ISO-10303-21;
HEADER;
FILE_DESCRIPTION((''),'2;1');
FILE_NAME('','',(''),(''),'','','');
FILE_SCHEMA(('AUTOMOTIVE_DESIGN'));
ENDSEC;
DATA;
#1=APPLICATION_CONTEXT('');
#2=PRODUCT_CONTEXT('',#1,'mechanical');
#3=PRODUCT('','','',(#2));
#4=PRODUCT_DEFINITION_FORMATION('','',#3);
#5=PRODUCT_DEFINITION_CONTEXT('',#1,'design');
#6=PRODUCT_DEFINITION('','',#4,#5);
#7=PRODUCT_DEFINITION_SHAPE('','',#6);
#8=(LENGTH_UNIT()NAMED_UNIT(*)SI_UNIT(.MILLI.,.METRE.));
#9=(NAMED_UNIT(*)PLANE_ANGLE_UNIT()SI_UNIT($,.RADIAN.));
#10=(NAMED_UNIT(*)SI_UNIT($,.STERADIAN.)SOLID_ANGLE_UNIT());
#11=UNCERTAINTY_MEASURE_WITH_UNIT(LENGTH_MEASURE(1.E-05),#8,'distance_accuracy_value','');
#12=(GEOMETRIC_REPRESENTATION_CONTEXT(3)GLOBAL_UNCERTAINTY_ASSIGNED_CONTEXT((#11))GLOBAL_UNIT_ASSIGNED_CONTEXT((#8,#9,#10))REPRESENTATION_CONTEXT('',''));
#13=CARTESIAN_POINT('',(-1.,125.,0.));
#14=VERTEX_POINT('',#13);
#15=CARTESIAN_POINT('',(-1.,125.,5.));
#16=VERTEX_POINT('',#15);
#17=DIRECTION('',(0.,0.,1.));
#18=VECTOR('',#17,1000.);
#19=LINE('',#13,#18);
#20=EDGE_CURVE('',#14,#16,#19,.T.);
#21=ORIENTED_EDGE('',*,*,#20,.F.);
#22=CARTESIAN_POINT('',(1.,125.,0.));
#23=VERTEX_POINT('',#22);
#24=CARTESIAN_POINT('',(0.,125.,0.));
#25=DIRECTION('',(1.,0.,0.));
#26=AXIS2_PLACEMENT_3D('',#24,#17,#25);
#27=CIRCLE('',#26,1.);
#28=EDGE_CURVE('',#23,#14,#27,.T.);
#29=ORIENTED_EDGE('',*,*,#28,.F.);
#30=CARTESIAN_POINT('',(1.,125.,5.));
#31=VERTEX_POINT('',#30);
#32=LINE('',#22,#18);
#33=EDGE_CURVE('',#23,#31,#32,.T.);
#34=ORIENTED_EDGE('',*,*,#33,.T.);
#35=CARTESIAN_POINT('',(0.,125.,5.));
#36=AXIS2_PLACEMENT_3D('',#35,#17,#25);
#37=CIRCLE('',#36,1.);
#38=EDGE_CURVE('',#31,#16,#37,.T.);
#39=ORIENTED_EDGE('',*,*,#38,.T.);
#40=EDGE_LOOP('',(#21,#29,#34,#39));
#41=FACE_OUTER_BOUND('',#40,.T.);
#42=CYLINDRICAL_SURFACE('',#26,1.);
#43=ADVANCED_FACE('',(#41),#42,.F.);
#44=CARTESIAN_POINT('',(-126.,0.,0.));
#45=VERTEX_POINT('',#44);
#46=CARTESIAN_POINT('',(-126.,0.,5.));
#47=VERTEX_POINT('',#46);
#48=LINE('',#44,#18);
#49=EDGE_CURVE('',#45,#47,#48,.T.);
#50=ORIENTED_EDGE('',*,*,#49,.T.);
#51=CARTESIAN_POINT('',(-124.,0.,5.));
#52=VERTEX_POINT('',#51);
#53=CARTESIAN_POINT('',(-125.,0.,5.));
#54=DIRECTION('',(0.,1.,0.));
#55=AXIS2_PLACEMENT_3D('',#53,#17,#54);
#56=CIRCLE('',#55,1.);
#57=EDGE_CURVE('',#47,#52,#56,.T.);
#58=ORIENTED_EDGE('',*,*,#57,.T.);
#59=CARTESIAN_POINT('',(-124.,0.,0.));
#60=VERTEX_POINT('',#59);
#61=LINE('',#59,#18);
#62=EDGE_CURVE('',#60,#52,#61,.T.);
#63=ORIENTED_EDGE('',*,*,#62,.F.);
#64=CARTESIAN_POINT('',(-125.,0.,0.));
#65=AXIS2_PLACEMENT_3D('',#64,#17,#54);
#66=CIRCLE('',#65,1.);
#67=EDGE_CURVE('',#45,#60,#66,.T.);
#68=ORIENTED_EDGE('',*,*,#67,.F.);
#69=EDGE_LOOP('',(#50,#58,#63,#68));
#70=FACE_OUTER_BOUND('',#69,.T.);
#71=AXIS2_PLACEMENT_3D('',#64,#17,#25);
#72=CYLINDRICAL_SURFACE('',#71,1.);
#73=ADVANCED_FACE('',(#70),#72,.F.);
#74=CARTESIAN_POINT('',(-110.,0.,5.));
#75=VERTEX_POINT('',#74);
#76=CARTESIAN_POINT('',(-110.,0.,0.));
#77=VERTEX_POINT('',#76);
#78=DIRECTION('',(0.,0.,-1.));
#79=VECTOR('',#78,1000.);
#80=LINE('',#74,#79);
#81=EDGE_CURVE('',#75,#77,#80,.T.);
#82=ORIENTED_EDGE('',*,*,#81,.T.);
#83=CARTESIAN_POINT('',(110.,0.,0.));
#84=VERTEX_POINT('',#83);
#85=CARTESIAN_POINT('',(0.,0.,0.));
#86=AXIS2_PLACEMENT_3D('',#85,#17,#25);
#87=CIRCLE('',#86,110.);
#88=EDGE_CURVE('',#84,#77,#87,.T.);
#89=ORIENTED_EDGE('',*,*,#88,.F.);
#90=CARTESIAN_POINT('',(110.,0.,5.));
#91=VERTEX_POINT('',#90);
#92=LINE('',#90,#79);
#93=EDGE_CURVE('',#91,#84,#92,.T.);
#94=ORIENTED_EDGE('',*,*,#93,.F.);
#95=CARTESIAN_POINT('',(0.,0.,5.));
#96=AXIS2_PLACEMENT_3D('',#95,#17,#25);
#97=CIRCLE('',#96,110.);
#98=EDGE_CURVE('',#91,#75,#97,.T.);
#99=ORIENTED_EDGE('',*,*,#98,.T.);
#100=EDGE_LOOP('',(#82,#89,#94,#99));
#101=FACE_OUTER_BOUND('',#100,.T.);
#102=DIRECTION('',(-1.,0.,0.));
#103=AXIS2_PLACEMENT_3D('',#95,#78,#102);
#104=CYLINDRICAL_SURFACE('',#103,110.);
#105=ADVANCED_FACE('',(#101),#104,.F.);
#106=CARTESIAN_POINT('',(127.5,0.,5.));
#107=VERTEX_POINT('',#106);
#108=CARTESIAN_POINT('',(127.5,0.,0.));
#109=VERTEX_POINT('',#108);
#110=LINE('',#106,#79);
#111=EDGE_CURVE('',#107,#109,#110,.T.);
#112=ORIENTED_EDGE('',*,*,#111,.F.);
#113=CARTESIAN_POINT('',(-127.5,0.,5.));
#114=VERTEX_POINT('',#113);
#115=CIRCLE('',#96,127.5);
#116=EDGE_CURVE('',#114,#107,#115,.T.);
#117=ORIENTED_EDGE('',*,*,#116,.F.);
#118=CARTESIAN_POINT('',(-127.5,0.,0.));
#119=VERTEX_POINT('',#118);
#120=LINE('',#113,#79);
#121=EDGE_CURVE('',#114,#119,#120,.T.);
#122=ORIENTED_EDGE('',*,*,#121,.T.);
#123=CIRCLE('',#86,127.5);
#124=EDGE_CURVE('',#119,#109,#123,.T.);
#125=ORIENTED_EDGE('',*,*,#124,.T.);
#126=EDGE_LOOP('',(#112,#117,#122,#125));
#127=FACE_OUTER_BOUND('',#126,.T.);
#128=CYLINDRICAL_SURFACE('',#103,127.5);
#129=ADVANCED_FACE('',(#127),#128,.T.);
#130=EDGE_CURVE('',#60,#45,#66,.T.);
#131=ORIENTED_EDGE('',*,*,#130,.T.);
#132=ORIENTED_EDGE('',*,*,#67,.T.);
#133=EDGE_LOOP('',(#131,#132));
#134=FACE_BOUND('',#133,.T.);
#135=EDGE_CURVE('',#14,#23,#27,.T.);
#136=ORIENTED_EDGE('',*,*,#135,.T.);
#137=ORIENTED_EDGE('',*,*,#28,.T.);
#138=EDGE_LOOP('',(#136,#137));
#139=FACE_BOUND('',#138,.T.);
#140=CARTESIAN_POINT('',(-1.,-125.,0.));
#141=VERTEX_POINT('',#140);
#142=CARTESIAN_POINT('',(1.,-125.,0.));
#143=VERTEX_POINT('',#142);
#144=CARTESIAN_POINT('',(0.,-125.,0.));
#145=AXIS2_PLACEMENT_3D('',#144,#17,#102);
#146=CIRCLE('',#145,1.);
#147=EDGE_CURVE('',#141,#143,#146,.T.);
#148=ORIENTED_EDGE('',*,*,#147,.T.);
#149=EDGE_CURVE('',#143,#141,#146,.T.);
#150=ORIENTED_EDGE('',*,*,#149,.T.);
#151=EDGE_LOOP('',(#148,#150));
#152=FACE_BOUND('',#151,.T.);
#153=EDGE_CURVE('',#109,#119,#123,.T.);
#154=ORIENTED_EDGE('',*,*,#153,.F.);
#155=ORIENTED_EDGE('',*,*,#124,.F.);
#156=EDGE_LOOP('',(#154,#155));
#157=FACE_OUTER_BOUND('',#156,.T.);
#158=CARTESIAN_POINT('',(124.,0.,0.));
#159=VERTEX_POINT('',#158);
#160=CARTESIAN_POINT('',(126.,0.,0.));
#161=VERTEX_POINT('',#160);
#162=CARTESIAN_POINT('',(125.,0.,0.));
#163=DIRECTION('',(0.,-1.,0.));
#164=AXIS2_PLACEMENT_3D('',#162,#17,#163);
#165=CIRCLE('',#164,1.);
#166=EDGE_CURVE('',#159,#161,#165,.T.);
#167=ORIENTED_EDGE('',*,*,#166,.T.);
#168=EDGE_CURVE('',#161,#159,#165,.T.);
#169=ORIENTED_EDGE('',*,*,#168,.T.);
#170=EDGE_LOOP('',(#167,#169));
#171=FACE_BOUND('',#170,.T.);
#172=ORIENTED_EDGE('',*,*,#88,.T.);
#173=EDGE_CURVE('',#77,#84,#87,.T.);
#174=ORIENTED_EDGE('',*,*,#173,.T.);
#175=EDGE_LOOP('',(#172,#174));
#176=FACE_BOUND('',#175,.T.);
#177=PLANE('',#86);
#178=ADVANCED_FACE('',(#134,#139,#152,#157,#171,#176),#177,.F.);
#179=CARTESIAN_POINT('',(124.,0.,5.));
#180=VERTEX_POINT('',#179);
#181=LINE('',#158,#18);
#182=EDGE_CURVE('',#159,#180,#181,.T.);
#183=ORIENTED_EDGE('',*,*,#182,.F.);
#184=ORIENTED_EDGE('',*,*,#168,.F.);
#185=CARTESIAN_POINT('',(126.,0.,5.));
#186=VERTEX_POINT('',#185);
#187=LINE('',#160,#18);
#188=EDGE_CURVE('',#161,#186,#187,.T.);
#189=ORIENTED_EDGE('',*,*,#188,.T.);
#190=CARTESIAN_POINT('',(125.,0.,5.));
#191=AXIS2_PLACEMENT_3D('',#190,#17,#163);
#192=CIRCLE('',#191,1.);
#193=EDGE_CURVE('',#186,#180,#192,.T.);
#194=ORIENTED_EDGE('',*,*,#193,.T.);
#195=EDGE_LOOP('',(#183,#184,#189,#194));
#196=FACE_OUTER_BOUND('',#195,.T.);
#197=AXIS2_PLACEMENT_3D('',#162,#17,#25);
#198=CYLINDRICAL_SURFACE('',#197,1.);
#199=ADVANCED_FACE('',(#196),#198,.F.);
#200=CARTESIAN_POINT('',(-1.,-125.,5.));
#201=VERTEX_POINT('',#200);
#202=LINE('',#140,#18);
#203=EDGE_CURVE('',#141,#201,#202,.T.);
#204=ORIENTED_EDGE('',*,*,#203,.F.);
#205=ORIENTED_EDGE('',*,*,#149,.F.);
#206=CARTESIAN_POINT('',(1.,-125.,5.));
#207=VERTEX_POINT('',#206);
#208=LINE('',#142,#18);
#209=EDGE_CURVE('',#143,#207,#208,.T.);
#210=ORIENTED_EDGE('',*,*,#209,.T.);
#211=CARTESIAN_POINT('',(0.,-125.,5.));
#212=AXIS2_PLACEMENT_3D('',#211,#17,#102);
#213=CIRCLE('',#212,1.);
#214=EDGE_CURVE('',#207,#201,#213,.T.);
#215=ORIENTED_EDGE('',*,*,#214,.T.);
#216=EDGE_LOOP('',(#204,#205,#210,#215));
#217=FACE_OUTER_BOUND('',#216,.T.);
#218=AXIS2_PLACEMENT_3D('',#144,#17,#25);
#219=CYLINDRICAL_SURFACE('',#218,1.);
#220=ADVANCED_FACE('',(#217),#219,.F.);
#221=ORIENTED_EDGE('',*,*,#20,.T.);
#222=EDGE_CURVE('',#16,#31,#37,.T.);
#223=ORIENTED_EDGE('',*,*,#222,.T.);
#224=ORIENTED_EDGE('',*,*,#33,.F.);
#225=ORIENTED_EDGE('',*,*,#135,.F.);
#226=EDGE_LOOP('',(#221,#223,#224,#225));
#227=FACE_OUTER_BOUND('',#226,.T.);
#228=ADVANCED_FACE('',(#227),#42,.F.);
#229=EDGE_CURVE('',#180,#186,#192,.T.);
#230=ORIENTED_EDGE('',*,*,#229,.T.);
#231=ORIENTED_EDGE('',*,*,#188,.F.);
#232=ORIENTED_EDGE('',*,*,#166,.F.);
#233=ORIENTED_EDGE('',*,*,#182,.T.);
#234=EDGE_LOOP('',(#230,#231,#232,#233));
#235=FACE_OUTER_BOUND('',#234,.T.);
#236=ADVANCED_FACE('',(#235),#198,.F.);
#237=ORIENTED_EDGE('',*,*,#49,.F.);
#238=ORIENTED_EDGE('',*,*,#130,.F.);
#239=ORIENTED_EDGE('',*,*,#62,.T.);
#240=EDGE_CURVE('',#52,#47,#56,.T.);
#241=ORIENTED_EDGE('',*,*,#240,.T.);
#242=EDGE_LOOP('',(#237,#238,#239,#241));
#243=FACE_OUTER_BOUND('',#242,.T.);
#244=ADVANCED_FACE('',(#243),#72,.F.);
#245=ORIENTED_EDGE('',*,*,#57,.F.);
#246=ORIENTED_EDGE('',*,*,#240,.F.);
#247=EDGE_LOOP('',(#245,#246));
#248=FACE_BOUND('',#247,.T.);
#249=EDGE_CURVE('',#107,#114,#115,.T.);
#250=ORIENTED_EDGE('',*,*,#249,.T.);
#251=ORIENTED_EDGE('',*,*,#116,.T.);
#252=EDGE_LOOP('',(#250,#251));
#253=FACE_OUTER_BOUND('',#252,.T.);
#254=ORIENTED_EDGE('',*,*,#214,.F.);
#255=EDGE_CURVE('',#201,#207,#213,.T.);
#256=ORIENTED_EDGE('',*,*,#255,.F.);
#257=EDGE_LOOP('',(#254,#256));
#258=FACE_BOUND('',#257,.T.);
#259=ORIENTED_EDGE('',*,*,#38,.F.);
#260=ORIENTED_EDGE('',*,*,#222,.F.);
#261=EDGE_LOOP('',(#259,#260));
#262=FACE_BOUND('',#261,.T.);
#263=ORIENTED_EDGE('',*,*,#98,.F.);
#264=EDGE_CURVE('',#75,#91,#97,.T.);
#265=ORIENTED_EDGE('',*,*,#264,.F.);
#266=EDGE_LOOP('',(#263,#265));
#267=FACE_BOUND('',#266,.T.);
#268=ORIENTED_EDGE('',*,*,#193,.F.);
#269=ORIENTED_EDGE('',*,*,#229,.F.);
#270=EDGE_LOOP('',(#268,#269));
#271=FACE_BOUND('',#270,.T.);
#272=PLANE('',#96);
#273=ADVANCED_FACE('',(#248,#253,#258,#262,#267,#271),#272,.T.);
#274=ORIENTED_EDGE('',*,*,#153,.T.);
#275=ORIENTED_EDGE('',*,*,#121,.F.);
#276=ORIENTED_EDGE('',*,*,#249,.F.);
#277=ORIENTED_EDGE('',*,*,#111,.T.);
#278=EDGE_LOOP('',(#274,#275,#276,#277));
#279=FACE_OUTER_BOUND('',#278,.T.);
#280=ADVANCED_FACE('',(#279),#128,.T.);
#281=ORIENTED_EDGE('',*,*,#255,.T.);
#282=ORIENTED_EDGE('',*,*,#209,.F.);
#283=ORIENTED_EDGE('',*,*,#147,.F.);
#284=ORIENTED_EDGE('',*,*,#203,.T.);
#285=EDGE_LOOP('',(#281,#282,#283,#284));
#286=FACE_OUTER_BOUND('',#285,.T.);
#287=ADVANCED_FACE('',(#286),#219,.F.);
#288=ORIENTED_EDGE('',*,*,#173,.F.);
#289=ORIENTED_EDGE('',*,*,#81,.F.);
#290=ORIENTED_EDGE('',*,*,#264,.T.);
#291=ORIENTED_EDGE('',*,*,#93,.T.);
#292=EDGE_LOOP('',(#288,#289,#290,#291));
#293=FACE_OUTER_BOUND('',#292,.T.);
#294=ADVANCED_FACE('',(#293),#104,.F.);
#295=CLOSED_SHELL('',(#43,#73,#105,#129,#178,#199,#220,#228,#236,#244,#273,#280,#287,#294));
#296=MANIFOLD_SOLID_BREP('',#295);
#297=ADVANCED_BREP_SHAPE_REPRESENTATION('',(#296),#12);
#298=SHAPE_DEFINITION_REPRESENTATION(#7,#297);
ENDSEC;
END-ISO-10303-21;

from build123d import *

# Parameters (mm, degrees)
SKETCH1_R           = 127.5
SKETCH1_R_2         = 110
BOSS_EXTRUDE1_DEPTH = 5
SKETCH4_R           = 1
CUT_EXTRUDE2_DEPTH  = 5
CIRPATTERN2_COUNT   = 4


with BuildPart() as part:
    # Sketch1 → Boss-Extrude1 (new body)
    with BuildSketch(Plane.XY):
        Circle(SKETCH1_R)
        Circle(SKETCH1_R_2, mode=Mode.SUBTRACT)
    extrude(amount=BOSS_EXTRUDE1_DEPTH)

    # Sketch4 → Cut-Extrude2 (cut)
    with BuildSketch(Plane.XY.offset(5)):
        with Locations((0, 125)):
            Circle(SKETCH4_R)
    cut_extrude2 = extrude(amount=-CUT_EXTRUDE2_DEPTH, mode=Mode.SUBTRACT)

    # CirPattern2: Cut-Extrude2 ×4 about axis
    cirpattern2_axis = Axis((0, 0, 0), (0, 0, 1))
    for i in range(1, CIRPATTERN2_COUNT):
        add(cut_extrude2.rotate(cirpattern2_axis, i * 360 / CIRPATTERN2_COUNT), mode=Mode.SUBTRACT)


solid = part.part
